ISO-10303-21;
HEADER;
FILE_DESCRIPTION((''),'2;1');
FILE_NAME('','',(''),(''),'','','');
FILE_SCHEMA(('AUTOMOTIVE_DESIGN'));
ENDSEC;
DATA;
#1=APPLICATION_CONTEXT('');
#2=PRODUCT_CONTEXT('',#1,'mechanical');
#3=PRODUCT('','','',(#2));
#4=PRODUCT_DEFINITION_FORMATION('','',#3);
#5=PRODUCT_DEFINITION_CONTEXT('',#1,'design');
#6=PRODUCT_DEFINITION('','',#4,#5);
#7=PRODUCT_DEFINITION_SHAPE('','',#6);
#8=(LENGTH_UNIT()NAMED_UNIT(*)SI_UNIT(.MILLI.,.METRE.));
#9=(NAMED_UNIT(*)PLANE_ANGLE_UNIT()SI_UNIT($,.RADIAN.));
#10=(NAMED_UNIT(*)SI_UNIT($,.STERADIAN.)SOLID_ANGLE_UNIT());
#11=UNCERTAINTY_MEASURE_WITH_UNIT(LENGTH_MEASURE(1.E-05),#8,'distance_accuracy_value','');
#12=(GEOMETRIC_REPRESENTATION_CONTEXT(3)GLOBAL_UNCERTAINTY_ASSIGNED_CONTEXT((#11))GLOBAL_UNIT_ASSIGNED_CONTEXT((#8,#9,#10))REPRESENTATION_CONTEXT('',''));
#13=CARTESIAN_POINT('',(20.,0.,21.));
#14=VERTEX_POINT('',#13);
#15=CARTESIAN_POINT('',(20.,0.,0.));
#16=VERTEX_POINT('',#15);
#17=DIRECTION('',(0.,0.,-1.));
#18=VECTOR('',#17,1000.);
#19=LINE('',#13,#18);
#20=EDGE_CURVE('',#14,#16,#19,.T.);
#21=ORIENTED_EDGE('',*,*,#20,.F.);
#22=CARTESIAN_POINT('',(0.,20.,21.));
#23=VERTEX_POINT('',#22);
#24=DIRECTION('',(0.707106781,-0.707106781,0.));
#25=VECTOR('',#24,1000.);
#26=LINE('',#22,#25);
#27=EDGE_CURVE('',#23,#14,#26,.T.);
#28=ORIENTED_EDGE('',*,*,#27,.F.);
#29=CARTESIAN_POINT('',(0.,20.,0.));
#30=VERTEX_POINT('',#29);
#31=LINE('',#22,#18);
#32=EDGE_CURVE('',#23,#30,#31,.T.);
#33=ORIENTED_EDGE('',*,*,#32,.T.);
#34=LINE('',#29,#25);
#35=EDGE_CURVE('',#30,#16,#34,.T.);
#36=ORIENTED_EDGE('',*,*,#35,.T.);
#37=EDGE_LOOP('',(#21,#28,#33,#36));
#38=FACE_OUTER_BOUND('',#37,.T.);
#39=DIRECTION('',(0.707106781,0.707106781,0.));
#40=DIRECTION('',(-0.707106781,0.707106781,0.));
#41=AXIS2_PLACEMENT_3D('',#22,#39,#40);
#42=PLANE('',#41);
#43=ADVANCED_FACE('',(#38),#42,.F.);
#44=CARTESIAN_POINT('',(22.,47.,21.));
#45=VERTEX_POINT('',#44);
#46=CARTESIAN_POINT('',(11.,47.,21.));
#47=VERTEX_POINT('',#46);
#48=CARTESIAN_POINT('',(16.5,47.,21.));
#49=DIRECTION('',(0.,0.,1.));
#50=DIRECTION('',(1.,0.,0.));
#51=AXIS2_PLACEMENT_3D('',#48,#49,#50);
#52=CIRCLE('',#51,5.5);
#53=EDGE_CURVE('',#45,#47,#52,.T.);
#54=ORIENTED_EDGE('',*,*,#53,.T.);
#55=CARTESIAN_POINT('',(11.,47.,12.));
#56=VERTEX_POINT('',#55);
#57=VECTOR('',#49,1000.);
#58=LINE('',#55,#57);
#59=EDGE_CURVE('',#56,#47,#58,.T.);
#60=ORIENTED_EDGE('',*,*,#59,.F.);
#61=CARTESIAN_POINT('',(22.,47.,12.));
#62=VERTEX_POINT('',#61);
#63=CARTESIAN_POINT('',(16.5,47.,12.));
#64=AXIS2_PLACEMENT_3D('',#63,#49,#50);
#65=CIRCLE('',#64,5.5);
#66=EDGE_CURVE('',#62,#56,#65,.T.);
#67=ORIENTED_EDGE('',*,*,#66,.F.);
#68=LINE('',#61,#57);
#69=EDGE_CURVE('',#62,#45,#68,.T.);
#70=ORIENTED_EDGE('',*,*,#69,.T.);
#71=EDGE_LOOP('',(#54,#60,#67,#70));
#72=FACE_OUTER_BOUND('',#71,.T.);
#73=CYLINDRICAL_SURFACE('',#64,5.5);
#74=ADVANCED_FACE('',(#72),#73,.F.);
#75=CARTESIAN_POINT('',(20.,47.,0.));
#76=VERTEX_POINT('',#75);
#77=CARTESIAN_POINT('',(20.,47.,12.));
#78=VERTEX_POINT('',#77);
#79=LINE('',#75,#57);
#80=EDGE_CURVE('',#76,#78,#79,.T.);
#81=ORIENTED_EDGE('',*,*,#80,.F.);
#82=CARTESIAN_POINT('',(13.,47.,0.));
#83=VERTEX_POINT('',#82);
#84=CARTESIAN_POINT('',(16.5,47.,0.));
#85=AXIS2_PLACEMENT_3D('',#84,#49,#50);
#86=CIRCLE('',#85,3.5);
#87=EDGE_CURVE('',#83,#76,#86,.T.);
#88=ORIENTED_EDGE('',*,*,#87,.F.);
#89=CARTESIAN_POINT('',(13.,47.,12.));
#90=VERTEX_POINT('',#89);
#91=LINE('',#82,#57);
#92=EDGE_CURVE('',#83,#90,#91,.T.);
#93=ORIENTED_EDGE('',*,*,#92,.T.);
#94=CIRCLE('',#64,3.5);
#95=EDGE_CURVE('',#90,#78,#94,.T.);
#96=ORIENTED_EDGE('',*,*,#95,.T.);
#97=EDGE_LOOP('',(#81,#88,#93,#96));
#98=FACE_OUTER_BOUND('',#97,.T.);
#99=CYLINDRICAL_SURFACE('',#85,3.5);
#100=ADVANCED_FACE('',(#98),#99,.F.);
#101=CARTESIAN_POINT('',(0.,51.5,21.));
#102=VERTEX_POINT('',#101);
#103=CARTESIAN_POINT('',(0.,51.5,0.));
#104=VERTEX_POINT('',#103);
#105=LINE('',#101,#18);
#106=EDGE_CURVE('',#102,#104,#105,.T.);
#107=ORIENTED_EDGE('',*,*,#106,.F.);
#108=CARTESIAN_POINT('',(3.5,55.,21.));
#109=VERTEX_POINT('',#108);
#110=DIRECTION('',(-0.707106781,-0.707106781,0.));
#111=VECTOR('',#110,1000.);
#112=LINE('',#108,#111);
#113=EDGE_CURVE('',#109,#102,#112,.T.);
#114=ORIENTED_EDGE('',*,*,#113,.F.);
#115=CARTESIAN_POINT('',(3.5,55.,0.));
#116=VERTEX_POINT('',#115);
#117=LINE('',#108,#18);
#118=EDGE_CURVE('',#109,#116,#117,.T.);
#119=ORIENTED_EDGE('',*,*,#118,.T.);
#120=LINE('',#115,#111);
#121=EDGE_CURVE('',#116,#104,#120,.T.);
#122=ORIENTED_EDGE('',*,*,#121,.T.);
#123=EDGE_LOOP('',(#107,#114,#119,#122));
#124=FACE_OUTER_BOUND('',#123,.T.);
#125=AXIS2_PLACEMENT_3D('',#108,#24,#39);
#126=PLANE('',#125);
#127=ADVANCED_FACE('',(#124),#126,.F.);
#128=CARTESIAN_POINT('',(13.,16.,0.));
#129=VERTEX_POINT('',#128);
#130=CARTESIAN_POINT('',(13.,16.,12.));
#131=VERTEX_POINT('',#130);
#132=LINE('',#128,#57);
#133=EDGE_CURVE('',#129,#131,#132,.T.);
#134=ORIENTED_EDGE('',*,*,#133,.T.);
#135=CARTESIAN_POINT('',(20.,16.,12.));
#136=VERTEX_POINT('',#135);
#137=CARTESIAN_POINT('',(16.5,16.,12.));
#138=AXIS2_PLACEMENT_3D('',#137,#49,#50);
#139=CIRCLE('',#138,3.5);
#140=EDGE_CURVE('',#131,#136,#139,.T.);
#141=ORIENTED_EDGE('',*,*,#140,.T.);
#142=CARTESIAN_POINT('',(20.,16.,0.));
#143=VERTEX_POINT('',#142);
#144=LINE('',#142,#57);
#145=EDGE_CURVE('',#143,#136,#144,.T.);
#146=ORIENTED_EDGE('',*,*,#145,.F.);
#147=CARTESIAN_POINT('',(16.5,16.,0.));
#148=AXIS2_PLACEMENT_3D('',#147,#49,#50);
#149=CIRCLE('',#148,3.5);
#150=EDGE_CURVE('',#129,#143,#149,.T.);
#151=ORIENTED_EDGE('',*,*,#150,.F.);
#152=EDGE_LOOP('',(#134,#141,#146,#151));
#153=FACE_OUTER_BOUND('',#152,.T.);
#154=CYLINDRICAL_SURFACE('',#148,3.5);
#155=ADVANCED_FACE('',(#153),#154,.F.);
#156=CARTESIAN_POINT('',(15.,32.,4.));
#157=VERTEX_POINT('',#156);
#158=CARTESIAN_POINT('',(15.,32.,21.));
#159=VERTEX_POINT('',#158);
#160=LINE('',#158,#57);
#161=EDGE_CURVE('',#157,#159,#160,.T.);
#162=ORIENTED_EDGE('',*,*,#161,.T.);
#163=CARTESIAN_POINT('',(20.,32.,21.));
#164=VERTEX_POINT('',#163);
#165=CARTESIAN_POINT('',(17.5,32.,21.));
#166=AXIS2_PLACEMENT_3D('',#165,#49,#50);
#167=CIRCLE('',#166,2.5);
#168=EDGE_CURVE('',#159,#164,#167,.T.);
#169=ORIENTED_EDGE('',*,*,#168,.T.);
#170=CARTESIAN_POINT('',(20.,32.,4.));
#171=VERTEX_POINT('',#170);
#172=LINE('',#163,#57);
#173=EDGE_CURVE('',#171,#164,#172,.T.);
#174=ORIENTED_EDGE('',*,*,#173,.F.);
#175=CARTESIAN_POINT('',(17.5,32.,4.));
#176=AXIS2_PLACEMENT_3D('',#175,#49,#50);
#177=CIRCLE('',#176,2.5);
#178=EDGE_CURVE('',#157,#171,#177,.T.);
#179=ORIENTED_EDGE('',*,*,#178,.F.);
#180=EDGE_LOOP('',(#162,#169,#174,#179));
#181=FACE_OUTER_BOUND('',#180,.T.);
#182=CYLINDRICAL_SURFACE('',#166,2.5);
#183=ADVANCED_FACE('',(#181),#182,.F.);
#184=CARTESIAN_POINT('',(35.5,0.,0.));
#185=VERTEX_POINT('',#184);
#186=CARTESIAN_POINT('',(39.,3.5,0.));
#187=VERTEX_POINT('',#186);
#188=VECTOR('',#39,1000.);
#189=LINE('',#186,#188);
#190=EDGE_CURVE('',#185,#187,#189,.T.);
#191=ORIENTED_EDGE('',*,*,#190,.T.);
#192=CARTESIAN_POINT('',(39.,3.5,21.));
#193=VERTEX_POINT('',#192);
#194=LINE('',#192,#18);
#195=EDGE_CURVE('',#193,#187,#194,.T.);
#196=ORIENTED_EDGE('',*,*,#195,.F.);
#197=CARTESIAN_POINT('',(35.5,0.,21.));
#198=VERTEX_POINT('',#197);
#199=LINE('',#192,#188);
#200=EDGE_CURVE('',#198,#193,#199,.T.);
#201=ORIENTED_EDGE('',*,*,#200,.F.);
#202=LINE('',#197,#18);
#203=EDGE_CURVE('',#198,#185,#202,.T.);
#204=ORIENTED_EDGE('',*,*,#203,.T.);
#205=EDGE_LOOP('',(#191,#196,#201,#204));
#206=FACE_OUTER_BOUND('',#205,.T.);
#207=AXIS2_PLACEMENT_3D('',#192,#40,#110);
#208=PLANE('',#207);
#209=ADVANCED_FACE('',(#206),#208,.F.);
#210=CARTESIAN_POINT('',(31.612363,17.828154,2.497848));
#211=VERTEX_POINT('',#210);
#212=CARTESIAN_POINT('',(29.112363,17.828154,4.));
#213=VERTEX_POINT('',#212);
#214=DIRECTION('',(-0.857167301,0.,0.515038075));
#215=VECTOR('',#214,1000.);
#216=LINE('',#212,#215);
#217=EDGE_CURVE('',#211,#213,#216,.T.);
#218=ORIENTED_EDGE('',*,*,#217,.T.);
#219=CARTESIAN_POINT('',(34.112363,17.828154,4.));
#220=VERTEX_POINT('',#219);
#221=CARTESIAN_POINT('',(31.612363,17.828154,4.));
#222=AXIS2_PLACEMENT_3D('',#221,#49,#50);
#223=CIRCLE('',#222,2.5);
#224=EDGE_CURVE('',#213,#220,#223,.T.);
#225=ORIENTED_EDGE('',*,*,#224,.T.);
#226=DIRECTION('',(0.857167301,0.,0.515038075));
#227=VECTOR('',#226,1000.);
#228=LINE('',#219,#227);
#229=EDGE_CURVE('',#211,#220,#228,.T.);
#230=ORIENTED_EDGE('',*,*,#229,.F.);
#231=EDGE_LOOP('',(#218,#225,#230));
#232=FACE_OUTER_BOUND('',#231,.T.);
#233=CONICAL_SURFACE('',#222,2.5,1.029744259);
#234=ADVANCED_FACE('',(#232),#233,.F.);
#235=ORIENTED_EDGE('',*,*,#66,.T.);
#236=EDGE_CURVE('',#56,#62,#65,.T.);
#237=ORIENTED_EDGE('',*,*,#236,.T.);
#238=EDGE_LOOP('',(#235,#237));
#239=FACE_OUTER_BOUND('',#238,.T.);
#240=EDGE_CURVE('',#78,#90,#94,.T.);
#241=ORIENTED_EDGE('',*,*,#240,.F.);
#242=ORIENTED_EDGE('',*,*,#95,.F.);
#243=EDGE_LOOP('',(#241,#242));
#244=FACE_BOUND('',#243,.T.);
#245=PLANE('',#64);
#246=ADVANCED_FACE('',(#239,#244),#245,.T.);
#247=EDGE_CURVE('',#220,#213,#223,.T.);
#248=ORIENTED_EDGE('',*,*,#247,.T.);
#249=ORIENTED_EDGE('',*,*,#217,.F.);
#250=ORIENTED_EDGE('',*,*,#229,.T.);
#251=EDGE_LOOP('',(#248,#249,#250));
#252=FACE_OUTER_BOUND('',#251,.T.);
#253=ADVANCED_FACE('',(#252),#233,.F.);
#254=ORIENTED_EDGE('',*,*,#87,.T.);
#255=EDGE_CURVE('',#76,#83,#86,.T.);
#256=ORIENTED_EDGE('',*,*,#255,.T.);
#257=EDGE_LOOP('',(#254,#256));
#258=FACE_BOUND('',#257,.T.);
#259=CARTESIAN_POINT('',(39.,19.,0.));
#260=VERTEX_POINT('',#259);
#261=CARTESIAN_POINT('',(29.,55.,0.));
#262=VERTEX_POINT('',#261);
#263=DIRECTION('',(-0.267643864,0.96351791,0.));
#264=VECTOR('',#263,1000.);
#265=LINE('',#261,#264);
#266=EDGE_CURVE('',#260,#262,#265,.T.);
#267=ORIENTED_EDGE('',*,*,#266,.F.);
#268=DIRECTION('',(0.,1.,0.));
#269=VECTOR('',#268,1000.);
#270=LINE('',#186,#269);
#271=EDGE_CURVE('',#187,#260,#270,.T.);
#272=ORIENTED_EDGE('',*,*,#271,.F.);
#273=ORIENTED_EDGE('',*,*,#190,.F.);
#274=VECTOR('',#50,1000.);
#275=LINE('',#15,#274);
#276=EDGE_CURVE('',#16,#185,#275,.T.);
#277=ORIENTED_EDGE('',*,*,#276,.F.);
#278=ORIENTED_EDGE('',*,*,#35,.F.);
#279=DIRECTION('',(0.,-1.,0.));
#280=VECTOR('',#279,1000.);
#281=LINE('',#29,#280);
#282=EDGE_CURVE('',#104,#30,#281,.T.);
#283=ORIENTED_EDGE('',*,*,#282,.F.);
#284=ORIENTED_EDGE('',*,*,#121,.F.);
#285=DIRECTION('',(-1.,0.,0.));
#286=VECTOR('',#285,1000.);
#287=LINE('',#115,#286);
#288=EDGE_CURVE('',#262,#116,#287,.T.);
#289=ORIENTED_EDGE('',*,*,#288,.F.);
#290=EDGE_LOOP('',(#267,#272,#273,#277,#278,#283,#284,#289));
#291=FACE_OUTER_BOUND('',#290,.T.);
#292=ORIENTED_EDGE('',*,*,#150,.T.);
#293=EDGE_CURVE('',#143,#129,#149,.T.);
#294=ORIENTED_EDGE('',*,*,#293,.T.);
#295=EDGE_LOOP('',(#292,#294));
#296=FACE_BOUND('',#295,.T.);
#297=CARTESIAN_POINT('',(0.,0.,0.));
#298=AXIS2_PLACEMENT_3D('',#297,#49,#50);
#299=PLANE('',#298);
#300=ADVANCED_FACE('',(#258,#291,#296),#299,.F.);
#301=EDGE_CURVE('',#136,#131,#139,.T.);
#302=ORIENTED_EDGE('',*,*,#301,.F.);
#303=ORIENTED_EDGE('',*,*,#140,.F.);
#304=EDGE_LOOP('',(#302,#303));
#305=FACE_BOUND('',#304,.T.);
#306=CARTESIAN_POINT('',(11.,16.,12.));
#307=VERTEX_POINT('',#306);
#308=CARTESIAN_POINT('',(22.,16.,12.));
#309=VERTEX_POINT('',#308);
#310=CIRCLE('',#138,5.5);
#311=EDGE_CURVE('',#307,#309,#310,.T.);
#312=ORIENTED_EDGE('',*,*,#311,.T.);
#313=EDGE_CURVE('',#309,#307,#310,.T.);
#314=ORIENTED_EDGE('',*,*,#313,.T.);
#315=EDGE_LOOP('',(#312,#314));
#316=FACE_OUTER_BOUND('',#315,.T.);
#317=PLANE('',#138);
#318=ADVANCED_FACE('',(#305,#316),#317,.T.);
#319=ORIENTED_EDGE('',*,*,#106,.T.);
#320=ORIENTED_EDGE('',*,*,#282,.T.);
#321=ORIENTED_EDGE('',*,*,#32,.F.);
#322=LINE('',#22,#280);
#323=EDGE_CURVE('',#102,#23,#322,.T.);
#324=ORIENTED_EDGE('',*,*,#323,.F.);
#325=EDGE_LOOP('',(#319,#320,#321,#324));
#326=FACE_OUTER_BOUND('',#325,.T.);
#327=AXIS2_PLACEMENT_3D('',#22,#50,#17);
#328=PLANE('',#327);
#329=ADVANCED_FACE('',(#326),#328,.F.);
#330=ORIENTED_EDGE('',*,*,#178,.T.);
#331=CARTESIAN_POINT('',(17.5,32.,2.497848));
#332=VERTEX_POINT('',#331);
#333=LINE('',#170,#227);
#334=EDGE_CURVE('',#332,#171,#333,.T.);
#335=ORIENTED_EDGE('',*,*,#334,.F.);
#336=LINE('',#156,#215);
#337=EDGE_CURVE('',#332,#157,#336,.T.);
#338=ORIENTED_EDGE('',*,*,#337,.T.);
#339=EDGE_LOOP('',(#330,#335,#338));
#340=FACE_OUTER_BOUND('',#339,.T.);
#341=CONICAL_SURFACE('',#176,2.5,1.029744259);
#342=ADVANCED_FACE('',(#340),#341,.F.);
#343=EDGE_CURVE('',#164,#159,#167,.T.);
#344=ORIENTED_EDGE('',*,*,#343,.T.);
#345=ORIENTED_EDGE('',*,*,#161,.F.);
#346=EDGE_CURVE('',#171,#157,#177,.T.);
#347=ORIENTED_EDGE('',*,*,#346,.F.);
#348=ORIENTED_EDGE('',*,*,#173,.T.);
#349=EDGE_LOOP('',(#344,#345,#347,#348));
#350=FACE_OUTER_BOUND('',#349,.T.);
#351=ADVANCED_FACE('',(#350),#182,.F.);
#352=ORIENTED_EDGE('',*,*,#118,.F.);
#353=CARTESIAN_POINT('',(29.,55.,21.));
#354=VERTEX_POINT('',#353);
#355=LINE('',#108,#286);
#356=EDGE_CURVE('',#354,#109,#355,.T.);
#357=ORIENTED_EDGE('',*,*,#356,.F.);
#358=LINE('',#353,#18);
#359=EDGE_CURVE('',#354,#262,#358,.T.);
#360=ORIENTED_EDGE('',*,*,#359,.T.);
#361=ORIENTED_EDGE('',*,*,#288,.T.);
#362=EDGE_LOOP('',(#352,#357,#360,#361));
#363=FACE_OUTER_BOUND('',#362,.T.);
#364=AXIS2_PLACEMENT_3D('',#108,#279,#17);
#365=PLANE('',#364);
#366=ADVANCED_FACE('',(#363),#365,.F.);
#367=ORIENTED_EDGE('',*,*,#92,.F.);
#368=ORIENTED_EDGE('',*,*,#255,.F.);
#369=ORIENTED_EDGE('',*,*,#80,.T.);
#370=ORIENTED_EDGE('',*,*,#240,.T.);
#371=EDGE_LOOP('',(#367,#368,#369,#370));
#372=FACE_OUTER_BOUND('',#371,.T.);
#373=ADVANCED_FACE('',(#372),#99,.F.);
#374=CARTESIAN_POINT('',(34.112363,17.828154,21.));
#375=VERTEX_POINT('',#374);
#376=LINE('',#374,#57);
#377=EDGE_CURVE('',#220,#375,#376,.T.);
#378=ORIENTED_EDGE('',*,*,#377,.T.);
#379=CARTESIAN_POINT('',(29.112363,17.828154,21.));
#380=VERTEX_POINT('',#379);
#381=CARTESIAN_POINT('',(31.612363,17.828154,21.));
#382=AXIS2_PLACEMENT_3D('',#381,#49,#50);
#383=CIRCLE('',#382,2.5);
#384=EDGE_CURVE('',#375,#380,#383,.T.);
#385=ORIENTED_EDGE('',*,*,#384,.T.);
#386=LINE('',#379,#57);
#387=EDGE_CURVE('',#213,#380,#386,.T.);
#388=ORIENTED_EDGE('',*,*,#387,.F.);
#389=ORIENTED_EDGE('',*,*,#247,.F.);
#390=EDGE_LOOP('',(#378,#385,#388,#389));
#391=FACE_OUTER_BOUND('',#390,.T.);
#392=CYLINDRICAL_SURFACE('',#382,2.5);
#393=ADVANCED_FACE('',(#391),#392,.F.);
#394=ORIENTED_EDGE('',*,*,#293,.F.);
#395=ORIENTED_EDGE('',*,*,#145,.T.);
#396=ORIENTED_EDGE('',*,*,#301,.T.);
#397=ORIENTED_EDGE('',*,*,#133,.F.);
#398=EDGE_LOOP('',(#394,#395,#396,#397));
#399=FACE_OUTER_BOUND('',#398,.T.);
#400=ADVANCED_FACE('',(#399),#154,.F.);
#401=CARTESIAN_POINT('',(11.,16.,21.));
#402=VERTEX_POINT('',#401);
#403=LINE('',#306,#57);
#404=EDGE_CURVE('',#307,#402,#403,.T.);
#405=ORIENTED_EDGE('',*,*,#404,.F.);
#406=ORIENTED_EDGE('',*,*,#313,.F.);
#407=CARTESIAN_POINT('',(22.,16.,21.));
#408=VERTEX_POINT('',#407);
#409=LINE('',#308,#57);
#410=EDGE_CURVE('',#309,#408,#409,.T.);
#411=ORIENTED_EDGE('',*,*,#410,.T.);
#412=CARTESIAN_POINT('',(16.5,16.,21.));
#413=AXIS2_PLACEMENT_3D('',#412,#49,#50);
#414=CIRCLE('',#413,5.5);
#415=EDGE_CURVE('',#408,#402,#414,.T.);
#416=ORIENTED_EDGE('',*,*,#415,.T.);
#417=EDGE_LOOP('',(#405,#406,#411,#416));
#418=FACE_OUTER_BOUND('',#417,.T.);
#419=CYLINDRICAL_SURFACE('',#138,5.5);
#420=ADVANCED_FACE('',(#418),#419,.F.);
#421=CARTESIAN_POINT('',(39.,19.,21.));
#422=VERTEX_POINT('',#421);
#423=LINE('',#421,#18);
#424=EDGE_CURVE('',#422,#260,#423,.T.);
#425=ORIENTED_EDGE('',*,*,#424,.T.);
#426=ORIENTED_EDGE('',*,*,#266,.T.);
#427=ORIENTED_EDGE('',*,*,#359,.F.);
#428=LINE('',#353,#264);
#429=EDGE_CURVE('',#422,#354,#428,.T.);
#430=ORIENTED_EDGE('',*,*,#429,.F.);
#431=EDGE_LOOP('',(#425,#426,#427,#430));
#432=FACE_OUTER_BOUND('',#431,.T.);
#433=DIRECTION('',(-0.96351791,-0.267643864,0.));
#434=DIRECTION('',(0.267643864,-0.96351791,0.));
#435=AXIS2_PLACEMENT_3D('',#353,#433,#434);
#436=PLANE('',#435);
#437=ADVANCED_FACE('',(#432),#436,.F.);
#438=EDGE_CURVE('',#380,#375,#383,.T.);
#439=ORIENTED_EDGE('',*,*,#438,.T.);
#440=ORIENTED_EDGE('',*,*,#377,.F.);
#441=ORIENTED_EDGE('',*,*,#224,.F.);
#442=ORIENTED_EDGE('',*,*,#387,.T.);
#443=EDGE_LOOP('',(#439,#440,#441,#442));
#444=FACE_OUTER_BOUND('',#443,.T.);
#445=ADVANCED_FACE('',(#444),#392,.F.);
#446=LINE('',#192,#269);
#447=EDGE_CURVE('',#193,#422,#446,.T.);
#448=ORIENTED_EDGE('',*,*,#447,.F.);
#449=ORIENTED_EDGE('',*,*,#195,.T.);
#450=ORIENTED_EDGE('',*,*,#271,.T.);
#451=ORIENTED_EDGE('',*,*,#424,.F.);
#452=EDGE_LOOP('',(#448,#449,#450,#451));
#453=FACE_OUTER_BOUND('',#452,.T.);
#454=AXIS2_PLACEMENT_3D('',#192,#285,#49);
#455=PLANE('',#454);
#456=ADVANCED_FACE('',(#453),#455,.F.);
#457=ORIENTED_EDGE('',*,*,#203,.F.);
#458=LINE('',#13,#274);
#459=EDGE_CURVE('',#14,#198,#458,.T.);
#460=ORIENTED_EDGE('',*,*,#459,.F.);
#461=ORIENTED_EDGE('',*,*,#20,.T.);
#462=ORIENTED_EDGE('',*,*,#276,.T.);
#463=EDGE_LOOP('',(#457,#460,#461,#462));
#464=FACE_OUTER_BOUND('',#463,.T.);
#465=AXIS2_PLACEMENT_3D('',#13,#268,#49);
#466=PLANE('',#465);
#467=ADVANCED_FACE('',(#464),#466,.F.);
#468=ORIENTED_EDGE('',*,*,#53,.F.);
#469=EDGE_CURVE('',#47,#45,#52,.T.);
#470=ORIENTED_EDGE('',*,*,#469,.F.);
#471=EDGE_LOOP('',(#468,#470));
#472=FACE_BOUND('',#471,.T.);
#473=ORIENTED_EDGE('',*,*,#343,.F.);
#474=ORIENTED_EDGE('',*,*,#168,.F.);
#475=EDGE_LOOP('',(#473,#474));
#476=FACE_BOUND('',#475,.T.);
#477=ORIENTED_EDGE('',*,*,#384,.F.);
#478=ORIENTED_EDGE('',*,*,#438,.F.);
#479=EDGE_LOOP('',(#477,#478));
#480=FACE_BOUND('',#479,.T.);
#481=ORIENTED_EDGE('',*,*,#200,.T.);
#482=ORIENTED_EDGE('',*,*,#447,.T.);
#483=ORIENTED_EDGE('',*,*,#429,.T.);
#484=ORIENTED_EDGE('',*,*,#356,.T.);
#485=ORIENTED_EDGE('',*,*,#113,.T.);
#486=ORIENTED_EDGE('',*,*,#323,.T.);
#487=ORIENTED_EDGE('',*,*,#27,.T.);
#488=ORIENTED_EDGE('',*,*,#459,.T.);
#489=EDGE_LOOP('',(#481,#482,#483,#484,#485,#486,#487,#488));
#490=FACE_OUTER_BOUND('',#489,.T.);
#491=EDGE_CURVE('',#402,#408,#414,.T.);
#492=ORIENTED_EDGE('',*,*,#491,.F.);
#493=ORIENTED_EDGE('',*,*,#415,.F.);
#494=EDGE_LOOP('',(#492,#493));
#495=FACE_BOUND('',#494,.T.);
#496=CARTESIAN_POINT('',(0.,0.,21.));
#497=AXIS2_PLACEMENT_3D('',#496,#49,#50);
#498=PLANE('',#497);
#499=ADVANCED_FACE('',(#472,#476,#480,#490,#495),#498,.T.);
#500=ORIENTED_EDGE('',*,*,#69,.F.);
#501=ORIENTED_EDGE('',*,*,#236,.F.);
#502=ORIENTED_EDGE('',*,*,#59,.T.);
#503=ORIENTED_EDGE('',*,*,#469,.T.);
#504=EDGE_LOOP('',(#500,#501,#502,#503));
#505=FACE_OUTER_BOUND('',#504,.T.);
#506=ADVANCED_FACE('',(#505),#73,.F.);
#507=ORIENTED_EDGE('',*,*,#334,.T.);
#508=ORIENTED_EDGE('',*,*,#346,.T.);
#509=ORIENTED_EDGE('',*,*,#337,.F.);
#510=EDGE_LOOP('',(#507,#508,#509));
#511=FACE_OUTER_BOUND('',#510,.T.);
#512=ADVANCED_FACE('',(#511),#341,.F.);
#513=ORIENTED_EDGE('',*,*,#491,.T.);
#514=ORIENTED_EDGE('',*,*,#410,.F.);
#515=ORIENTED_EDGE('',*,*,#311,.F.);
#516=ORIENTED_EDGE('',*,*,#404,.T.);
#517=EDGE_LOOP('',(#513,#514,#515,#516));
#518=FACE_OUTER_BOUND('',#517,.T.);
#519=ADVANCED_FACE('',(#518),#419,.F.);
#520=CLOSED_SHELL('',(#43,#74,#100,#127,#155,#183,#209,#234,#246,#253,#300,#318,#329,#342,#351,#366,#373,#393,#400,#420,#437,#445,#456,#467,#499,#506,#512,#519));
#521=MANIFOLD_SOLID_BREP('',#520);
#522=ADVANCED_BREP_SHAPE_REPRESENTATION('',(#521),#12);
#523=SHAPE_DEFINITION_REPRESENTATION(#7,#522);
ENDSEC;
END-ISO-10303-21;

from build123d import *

# Parameters (mm, degrees)
EXTRUDE_1_DEPTH        = 21
SKETCH_2_R             = 5.5
CUT_EXTRUDE_1_DEPTH    = 9
SKETCH_3_R             = 3.5
CUT_EXTRUDE_2_DEPTH    = 69.483574673
HOLE_WIZARD_M6_1_D     = 5
HOLE_WIZARD_M6_1_DEPTH = 17
HOLE_WIZARD_M6_1_TIP   = 1.502151548


with BuildPart() as part:
    # 草图1 → 凸台-拉伸1 (new body)
    with BuildSketch(Plane.XY):
        Polygon((0, 20), (20, 0), (35.5, 0), (39, 3.5), (39, 19), (29, 55), (3.5, 55), (0, 51.5), align=None)
    extrude(amount=EXTRUDE_1_DEPTH)

    # 草图2 → 切除-拉伸1 (cut)
    with BuildSketch(Plane.XY.offset(21)):
        with Locations((16.5, 47)):
            Circle(SKETCH_2_R)
        with Locations((16.5, 16)):
            Circle(SKETCH_2_R)
    extrude(amount=-CUT_EXTRUDE_1_DEPTH, mode=Mode.SUBTRACT)

    # 草图3 → 切除-拉伸2 (cut, through all)
    with BuildSketch(Plane.XY.offset(12)):
        with Locations((16.5, 47)):
            Circle(SKETCH_3_R)
        with Locations((16.5, 16)):
            Circle(SKETCH_3_R)
    extrude(amount=-CUT_EXTRUDE_2_DEPTH, mode=Mode.SUBTRACT)

    # M6 螺纹孔1
    with Locations(Plane(origin=(17.5, 32, 21), x_dir=(1, 0, 0), z_dir=(0, 0, 1))):
        with Locations((0, 0), (14.112362721, -14.171845978)):
            Hole(HOLE_WIZARD_M6_1_D / 2, depth=HOLE_WIZARD_M6_1_DEPTH)
            with Locations((0, 0, -(HOLE_WIZARD_M6_1_DEPTH + HOLE_WIZARD_M6_1_TIP / 2))):  # 118° drill point
                Cone(0, HOLE_WIZARD_M6_1_D / 2, HOLE_WIZARD_M6_1_TIP, mode=Mode.SUBTRACT)


solid = part.part
